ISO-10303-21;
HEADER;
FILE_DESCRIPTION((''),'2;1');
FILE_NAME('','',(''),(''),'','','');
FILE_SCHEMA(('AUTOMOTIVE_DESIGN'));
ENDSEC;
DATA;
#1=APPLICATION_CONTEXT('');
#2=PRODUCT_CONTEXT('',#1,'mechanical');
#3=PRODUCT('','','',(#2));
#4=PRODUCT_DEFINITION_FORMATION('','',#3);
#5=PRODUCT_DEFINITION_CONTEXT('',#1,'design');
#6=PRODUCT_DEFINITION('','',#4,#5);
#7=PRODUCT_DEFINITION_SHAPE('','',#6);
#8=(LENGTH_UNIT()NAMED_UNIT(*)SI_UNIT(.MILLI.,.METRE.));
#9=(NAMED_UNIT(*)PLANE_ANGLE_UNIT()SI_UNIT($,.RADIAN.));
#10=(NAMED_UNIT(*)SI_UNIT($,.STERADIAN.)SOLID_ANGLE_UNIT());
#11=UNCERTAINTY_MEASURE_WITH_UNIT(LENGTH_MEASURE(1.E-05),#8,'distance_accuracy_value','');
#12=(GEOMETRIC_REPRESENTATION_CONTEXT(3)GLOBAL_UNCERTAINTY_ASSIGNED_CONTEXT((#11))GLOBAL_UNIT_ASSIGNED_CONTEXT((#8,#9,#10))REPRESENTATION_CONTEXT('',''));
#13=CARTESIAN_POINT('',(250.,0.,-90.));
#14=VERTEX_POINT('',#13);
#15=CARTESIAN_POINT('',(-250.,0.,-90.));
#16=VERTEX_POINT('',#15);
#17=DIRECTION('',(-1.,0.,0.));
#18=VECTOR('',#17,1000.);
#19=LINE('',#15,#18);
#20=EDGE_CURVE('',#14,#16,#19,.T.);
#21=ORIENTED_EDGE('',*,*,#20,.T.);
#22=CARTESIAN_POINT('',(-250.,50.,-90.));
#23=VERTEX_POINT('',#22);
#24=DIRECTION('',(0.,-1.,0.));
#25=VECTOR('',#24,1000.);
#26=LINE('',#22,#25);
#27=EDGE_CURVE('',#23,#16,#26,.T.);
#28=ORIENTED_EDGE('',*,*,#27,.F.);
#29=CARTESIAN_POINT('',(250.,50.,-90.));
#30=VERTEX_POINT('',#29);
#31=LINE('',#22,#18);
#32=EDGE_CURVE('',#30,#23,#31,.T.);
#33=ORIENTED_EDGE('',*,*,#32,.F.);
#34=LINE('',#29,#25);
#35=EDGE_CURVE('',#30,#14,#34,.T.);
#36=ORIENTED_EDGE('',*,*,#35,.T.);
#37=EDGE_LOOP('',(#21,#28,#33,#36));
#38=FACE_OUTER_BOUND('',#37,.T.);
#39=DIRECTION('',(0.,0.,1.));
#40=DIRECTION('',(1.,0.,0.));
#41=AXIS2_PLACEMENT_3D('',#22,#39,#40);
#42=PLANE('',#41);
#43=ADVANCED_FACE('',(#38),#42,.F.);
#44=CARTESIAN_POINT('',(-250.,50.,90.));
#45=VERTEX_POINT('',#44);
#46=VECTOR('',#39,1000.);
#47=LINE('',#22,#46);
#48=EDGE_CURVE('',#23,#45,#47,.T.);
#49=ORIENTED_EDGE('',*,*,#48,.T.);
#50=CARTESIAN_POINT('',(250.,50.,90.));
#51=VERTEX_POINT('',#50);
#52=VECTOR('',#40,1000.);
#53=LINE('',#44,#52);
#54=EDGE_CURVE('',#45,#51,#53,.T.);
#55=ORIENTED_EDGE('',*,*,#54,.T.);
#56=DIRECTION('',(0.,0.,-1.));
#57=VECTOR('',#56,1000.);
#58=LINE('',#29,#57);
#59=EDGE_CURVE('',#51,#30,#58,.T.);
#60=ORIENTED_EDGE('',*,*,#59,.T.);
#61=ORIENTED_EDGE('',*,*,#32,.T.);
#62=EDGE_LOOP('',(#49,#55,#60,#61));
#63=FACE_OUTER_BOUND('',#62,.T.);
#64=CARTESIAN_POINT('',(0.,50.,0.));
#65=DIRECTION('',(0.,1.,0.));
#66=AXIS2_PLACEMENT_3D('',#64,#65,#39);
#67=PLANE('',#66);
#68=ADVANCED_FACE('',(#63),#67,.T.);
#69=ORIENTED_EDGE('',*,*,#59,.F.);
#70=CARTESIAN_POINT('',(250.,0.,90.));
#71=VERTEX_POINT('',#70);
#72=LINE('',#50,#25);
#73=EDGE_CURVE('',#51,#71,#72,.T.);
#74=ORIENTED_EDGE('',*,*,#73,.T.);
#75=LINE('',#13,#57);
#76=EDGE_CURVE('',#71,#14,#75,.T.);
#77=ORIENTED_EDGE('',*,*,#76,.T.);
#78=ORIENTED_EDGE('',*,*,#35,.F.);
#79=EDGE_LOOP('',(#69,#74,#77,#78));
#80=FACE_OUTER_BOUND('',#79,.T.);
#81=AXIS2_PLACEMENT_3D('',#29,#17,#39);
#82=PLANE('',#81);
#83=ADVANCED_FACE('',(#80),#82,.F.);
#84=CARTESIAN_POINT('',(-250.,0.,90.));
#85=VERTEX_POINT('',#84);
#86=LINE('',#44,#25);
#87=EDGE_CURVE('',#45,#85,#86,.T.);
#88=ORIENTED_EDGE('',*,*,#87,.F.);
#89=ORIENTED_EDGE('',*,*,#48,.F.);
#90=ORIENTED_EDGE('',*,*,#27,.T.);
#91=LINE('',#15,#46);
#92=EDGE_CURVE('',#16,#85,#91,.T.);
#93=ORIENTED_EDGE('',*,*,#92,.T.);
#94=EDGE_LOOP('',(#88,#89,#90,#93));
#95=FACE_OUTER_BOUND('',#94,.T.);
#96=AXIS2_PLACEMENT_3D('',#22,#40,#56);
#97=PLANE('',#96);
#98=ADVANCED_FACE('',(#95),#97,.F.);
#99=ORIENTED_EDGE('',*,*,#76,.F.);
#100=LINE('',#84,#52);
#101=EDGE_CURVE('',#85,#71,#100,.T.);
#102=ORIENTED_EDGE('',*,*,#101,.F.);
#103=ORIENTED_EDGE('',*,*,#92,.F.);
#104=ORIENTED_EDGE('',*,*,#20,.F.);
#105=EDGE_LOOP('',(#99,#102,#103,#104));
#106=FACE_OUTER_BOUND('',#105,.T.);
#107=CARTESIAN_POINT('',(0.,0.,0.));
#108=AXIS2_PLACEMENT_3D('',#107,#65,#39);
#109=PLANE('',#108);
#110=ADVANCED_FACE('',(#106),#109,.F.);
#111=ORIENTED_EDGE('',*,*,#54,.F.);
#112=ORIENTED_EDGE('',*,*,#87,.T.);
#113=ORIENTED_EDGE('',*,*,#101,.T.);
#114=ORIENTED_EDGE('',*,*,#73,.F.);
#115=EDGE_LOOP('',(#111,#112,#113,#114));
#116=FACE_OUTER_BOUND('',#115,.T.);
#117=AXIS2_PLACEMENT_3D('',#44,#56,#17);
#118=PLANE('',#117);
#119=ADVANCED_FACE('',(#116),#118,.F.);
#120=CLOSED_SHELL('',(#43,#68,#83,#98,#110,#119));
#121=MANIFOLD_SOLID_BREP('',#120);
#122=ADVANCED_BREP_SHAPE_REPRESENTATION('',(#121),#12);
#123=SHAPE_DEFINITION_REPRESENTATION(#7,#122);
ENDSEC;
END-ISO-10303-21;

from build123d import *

# Parameters (mm, degrees)
SKETCH_1_W      = 500
SKETCH_1_H      = 180
EXTRUDE_1_DEPTH = 50


with BuildPart() as part:
    # 草图1 → 凸台-拉伸1 (new body)
    with BuildSketch(Plane(origin=(0, 0, 0), x_dir=(1, 0, 0), z_dir=(0, 1, 0))):
        Rectangle(SKETCH_1_W, SKETCH_1_H)
    extrude(amount=EXTRUDE_1_DEPTH)


solid = part.part
